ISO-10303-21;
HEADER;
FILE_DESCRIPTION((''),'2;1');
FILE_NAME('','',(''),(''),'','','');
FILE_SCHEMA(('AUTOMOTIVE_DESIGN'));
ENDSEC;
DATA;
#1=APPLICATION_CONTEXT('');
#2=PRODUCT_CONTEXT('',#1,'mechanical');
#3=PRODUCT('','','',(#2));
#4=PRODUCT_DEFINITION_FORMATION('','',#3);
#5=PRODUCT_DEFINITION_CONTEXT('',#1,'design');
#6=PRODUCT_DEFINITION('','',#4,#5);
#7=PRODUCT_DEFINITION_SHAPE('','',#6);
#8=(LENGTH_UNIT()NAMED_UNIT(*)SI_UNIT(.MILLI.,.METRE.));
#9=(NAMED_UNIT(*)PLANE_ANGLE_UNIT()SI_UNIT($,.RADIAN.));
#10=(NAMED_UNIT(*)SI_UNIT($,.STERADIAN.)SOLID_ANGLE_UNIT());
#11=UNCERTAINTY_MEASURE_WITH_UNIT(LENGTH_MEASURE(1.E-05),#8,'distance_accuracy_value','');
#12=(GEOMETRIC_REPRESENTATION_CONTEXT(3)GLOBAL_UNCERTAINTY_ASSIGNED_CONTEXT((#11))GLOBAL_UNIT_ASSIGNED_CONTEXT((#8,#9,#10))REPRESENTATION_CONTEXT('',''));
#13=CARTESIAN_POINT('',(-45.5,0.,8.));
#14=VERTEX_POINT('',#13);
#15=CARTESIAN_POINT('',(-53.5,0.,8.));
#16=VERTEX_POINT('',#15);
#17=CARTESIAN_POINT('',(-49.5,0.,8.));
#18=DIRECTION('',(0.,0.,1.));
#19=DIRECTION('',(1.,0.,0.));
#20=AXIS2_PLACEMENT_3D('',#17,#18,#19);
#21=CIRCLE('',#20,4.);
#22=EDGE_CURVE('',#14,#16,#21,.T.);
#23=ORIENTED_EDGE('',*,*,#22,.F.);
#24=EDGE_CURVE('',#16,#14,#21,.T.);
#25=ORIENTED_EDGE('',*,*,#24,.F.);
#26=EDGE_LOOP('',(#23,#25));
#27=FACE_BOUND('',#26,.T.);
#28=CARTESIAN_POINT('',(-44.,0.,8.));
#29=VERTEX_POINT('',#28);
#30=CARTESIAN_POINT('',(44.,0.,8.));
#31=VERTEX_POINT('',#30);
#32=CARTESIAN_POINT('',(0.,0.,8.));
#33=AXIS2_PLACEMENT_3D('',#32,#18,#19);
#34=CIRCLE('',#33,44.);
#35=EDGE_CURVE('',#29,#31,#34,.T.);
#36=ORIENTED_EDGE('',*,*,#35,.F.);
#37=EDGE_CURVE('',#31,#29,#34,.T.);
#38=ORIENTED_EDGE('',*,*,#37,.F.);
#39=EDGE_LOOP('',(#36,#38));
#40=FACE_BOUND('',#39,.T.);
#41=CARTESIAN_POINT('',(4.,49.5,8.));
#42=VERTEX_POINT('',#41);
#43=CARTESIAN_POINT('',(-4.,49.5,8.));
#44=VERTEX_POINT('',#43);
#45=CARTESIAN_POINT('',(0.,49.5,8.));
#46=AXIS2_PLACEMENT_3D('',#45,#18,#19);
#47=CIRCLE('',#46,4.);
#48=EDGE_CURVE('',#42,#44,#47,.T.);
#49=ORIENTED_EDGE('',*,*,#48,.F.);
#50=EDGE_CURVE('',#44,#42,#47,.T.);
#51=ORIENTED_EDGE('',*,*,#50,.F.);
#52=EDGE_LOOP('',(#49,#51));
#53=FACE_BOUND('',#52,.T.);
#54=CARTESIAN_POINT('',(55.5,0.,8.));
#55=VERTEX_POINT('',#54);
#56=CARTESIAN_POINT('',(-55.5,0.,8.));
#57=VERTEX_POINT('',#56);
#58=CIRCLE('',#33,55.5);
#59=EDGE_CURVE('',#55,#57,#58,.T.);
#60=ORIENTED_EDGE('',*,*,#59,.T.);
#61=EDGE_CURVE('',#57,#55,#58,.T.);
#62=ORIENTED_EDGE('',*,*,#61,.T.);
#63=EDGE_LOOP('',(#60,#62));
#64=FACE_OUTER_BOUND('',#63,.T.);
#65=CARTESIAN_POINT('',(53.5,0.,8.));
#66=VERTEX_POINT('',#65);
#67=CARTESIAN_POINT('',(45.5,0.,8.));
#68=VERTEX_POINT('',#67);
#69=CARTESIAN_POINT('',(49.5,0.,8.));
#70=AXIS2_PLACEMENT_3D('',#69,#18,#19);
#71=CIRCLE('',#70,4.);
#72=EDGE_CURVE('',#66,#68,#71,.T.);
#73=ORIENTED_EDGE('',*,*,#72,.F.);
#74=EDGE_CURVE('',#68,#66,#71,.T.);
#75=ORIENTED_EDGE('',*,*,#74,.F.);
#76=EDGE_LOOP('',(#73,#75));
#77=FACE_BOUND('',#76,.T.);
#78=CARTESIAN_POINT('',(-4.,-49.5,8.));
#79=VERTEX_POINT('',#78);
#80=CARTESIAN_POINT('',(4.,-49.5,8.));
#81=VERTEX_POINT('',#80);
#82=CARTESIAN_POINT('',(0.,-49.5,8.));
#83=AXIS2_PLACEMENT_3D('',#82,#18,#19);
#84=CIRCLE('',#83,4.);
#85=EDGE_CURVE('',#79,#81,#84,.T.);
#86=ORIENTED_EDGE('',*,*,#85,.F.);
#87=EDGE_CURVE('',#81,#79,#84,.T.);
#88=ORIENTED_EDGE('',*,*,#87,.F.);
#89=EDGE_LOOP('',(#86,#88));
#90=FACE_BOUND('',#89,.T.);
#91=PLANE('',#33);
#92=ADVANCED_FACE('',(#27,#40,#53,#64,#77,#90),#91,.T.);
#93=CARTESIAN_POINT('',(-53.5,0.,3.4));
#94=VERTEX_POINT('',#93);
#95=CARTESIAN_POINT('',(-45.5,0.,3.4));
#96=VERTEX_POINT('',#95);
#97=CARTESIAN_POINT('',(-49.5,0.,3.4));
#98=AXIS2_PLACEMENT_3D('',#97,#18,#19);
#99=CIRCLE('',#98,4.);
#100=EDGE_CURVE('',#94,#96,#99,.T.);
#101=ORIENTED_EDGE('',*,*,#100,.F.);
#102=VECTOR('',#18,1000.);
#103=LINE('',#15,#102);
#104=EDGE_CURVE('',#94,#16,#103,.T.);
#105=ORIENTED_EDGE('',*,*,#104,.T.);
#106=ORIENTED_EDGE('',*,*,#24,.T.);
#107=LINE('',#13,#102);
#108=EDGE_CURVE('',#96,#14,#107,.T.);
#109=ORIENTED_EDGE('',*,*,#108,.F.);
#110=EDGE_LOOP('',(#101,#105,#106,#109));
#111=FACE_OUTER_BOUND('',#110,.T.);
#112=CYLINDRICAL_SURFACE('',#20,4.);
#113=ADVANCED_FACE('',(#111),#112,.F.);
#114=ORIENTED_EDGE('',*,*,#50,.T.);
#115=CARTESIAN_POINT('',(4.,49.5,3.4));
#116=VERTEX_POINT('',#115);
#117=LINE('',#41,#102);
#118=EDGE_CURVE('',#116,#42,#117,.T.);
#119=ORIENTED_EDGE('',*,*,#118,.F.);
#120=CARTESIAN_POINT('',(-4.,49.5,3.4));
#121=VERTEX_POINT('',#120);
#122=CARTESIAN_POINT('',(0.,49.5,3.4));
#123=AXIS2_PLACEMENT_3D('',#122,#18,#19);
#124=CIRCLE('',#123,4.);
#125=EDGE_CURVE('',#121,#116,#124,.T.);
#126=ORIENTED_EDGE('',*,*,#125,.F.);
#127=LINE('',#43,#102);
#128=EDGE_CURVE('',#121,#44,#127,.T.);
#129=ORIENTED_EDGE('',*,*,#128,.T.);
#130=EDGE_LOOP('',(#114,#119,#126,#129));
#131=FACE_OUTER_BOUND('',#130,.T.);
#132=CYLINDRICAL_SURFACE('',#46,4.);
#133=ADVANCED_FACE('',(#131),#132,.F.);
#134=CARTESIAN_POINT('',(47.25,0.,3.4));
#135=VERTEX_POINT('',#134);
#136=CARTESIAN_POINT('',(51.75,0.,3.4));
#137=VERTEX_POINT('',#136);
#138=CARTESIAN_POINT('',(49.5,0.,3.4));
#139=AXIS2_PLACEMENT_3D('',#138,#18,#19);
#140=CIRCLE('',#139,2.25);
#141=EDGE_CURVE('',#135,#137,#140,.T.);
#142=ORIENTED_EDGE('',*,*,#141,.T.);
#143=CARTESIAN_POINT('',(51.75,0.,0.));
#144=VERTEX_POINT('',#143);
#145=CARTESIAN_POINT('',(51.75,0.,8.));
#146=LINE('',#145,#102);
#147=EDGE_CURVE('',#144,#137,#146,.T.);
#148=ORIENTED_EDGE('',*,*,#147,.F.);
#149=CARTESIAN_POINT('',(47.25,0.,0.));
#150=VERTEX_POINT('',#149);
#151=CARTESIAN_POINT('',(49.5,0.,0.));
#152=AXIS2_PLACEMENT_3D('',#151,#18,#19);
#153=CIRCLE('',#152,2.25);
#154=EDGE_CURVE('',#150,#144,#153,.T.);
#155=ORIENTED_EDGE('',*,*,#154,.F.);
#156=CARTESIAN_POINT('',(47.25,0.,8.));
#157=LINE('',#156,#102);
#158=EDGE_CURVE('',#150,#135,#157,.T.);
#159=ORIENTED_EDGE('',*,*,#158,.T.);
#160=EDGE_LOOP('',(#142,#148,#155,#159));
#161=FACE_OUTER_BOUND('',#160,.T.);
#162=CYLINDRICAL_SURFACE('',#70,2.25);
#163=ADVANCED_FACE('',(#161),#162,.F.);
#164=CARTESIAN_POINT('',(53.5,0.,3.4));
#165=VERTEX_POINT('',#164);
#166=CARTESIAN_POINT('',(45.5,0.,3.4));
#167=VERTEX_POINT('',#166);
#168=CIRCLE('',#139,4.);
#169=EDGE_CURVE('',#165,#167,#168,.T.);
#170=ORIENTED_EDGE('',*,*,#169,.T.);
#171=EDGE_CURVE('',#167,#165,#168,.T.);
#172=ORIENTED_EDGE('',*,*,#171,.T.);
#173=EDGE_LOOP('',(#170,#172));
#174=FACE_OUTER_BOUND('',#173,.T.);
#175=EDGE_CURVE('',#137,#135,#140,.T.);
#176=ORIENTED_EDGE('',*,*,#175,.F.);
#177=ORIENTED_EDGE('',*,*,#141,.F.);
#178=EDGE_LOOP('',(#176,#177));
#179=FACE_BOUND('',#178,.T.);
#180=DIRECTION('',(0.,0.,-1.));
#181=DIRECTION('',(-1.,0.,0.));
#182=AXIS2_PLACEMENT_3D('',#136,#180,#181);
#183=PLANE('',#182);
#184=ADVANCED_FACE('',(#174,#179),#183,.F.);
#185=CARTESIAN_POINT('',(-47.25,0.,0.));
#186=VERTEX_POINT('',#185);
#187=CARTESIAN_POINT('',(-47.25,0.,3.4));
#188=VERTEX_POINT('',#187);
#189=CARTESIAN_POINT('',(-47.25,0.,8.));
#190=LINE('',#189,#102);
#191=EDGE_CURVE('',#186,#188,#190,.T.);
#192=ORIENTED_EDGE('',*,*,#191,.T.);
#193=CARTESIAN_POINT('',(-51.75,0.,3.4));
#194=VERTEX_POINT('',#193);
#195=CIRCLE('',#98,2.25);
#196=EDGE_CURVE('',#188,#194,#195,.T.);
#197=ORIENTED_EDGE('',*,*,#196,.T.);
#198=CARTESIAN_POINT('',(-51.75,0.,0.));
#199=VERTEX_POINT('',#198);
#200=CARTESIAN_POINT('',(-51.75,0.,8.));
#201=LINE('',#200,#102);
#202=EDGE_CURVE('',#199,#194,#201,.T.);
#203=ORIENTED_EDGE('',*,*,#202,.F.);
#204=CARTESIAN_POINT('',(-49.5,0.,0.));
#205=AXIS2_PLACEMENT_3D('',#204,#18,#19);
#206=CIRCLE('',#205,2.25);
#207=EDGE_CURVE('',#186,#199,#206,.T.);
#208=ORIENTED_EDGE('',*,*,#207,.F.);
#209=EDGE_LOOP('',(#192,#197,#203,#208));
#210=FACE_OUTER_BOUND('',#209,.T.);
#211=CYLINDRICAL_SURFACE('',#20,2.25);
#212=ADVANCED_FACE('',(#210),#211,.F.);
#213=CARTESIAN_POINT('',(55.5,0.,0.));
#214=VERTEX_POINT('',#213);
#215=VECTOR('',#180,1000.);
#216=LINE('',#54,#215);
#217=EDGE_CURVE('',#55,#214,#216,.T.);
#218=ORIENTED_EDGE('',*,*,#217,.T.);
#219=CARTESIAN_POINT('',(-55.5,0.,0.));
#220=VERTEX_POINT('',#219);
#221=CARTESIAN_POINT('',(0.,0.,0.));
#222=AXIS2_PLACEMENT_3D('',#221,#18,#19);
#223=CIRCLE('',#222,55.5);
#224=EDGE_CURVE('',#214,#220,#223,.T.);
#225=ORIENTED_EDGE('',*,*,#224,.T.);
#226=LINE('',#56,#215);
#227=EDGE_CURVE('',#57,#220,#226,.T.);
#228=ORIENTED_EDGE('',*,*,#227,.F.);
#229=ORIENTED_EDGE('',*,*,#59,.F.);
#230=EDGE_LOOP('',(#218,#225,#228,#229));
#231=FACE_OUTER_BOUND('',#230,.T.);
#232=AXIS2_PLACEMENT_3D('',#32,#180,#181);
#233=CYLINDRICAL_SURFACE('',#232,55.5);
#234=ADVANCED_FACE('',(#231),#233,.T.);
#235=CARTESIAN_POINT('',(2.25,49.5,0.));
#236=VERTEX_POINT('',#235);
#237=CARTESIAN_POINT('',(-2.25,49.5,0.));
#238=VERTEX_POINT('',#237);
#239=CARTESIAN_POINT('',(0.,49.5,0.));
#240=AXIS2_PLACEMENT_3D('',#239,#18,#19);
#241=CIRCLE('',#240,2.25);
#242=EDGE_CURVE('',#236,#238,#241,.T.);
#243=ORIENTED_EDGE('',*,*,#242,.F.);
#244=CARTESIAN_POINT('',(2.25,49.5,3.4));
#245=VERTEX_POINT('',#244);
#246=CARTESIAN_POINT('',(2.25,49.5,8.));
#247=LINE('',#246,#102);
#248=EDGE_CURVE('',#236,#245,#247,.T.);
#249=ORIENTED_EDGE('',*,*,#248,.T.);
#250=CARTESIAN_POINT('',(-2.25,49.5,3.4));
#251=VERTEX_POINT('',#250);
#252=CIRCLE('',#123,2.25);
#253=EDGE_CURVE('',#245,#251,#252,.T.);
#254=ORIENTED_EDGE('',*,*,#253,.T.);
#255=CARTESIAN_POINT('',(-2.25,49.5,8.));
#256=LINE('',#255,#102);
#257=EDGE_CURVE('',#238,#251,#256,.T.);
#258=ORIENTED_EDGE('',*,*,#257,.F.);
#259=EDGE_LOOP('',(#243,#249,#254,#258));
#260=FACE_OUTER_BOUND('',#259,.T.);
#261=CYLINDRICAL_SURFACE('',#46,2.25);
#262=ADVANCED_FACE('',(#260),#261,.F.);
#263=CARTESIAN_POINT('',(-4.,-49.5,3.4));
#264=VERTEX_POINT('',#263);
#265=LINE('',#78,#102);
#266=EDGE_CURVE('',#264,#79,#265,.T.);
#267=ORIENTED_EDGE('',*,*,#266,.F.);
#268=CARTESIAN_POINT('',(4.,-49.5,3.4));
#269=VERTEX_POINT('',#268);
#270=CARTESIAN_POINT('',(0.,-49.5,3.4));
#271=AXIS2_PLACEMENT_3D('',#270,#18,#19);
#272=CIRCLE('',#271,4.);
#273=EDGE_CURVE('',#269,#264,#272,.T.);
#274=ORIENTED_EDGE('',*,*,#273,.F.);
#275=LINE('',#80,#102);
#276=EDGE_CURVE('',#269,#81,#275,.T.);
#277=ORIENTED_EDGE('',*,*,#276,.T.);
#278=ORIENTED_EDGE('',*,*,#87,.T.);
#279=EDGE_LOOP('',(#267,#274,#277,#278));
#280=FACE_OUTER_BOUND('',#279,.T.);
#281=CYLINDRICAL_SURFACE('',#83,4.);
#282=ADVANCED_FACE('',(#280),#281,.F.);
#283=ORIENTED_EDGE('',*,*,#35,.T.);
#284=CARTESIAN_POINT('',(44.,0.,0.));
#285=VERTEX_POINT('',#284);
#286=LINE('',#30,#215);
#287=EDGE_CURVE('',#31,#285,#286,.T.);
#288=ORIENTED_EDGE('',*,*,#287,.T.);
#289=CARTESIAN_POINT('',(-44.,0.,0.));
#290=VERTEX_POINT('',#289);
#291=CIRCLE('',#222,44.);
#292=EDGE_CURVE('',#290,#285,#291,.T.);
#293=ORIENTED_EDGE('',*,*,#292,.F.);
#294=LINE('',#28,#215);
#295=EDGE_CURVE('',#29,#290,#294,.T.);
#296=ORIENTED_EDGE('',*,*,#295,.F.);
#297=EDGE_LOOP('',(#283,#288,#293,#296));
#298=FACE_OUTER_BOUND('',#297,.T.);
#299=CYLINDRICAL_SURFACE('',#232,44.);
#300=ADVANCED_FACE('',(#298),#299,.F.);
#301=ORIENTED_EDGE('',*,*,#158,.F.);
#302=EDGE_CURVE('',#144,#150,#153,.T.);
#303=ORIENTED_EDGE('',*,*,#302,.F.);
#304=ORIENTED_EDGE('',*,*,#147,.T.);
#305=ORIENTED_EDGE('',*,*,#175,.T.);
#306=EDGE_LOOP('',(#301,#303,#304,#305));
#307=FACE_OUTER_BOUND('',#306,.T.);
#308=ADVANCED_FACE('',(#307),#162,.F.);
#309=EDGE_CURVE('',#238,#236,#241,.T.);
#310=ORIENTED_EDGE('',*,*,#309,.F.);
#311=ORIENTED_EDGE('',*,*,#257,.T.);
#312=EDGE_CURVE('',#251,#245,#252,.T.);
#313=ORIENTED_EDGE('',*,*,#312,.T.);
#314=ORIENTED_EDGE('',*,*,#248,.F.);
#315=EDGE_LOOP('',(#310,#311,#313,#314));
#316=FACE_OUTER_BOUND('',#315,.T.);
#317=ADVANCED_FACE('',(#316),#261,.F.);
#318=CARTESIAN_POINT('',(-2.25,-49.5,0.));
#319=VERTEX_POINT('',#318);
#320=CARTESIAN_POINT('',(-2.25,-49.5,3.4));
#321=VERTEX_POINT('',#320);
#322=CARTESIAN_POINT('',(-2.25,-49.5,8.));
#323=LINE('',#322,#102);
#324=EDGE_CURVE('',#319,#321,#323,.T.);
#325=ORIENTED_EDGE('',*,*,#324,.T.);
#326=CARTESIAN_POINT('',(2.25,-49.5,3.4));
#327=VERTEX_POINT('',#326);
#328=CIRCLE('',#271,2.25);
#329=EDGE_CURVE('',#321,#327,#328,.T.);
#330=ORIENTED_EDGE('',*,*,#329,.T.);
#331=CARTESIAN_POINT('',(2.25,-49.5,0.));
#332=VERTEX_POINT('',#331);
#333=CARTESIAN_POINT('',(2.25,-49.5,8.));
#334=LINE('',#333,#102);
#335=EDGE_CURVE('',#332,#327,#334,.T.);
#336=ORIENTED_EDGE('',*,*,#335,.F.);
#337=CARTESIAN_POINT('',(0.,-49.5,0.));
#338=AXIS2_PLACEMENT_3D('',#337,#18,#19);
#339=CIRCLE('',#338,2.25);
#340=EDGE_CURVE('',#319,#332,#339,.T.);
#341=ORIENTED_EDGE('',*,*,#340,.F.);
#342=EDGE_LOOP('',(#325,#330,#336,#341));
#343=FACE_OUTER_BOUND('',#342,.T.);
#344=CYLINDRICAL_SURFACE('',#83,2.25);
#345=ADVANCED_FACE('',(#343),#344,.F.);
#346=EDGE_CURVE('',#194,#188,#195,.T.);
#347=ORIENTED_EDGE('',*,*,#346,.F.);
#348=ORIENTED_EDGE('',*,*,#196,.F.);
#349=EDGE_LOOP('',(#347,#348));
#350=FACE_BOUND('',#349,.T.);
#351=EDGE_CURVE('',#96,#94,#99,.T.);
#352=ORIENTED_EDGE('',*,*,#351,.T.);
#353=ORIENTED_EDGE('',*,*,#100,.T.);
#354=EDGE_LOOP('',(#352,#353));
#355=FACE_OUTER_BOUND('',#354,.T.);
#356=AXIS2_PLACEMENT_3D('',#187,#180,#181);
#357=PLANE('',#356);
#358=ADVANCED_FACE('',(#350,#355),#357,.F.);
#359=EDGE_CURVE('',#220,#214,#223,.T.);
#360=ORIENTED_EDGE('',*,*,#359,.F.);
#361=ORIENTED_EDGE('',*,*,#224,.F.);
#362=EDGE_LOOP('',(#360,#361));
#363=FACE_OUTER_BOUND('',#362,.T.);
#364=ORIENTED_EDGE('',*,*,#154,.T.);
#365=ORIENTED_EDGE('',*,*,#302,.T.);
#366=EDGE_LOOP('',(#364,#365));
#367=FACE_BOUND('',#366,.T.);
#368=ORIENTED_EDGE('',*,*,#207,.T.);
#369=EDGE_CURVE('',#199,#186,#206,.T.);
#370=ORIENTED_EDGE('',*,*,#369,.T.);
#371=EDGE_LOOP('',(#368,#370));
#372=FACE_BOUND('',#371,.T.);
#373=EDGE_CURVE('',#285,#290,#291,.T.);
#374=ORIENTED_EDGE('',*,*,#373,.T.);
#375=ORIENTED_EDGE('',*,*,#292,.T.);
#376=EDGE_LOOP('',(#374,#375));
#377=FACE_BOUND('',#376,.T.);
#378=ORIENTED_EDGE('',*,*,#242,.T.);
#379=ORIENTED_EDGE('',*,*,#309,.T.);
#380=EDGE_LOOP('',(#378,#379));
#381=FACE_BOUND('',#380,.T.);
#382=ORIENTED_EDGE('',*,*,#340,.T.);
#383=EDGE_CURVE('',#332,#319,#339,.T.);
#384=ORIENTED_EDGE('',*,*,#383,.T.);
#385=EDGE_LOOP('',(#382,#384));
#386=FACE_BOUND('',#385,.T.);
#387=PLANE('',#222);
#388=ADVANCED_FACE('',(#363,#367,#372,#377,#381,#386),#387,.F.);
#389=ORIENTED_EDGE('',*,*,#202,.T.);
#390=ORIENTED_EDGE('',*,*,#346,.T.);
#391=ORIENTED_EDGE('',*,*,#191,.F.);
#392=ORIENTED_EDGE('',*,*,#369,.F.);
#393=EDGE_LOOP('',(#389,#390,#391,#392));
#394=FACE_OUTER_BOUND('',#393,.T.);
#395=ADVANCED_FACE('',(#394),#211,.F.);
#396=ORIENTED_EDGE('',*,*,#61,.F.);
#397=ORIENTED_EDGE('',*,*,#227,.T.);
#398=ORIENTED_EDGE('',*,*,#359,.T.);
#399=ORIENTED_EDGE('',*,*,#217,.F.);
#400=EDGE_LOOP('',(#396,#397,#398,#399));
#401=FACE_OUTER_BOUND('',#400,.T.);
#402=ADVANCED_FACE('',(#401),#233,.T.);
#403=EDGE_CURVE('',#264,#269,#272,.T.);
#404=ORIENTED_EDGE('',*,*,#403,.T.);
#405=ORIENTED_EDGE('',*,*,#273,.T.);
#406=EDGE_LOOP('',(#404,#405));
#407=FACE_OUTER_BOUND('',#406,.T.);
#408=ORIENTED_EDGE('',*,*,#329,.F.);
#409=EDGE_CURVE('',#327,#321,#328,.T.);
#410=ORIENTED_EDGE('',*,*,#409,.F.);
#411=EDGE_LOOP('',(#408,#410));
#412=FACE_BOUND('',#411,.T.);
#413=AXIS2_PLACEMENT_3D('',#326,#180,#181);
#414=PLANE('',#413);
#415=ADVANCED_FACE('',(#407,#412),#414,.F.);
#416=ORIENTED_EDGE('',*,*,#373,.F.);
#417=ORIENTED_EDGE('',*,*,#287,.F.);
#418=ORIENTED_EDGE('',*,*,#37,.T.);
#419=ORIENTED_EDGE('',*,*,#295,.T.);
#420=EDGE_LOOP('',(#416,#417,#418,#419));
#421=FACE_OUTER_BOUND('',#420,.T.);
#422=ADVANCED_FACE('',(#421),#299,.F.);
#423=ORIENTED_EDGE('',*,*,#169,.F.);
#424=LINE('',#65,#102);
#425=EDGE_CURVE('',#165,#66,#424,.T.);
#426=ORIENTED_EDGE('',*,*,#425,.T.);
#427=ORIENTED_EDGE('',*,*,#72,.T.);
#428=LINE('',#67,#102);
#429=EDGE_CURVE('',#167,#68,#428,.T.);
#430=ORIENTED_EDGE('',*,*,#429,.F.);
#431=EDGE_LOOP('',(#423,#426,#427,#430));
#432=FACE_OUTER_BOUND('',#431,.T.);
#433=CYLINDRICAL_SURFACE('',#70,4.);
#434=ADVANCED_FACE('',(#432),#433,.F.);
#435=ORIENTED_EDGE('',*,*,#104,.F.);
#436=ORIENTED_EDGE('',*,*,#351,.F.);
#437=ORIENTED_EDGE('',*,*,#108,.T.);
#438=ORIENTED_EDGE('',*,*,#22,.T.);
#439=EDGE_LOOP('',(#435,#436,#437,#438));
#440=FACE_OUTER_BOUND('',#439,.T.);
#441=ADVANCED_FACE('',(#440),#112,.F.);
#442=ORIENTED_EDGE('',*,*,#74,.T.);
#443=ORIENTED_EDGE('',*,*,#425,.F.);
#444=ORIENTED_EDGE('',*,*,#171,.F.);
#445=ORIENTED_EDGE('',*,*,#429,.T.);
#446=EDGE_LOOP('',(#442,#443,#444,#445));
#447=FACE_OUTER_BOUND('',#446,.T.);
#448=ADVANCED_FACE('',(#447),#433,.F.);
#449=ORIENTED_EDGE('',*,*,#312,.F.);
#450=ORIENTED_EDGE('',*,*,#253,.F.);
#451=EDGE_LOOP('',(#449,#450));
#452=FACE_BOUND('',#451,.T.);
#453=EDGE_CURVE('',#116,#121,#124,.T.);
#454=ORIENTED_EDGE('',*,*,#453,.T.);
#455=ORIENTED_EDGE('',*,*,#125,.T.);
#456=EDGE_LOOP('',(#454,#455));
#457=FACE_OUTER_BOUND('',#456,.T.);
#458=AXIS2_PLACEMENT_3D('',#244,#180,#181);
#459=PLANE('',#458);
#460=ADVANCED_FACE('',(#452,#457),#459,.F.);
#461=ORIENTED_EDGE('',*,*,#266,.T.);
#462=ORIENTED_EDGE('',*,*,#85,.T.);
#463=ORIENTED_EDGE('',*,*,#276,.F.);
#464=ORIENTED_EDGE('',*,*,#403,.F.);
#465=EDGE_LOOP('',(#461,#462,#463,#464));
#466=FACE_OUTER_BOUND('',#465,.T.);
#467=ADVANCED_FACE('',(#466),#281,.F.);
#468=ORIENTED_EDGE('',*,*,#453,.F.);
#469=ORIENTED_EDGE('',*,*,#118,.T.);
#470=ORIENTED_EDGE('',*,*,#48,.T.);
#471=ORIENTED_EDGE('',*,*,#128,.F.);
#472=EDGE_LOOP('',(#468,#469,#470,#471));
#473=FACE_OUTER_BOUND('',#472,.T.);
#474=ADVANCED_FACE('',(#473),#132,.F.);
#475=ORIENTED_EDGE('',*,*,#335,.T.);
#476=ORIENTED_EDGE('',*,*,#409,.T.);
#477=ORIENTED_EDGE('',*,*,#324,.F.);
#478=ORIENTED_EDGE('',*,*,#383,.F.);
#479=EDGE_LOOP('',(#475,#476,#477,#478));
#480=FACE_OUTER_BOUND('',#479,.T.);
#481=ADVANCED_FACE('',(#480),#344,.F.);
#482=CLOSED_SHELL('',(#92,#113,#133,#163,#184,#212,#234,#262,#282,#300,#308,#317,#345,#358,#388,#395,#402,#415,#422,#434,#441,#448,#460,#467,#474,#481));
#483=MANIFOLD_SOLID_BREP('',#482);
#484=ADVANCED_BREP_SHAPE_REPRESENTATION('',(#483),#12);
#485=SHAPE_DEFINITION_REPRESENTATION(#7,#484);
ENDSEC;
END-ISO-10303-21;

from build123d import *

# Parameters (mm, degrees)
SKETCH1_R           = 55.5
SKETCH1_R_2         = 44
BOSS_EXTRUDE1_DEPTH = 8
CIRPATTERN1_COUNT   = 4


with BuildPart() as part:
    # Sketch1 → Boss-Extrude1 (new body)
    with BuildSketch(Plane.XY):
        Circle(SKETCH1_R)
        Circle(SKETCH1_R_2, mode=Mode.SUBTRACT)
    extrude(amount=BOSS_EXTRUDE1_DEPTH)

    # Sketch5 → Hole size per socket head cap screw type 1 (revolve, cut)
    with BuildSketch(Plane(origin=(0, 49.5, 8), x_dir=(0, -1, 0), z_dir=(1, 0, 0))):
        Polygon((0, 0), (0, 18.351936393), (2.25, 17), (2.25, 4.6), (4, 4.6), (4, 0), align=None)
    hole_size_per_socket_head_cap_screw_type = revolve(axis=Axis((0, 49.5, 14.35), (0, 0, -1)), mode=Mode.SUBTRACT)

    # CirPattern1: Hole size per socket head cap screw type 1 ×4 about axis
    cirpattern1_axis = Axis((0, 0, 0), (0, 0, 1))
    for i in range(1, CIRPATTERN1_COUNT):
        add(hole_size_per_socket_head_cap_screw_type.rotate(cirpattern1_axis, i * 360 / CIRPATTERN1_COUNT), mode=Mode.SUBTRACT)


solid = part.part
